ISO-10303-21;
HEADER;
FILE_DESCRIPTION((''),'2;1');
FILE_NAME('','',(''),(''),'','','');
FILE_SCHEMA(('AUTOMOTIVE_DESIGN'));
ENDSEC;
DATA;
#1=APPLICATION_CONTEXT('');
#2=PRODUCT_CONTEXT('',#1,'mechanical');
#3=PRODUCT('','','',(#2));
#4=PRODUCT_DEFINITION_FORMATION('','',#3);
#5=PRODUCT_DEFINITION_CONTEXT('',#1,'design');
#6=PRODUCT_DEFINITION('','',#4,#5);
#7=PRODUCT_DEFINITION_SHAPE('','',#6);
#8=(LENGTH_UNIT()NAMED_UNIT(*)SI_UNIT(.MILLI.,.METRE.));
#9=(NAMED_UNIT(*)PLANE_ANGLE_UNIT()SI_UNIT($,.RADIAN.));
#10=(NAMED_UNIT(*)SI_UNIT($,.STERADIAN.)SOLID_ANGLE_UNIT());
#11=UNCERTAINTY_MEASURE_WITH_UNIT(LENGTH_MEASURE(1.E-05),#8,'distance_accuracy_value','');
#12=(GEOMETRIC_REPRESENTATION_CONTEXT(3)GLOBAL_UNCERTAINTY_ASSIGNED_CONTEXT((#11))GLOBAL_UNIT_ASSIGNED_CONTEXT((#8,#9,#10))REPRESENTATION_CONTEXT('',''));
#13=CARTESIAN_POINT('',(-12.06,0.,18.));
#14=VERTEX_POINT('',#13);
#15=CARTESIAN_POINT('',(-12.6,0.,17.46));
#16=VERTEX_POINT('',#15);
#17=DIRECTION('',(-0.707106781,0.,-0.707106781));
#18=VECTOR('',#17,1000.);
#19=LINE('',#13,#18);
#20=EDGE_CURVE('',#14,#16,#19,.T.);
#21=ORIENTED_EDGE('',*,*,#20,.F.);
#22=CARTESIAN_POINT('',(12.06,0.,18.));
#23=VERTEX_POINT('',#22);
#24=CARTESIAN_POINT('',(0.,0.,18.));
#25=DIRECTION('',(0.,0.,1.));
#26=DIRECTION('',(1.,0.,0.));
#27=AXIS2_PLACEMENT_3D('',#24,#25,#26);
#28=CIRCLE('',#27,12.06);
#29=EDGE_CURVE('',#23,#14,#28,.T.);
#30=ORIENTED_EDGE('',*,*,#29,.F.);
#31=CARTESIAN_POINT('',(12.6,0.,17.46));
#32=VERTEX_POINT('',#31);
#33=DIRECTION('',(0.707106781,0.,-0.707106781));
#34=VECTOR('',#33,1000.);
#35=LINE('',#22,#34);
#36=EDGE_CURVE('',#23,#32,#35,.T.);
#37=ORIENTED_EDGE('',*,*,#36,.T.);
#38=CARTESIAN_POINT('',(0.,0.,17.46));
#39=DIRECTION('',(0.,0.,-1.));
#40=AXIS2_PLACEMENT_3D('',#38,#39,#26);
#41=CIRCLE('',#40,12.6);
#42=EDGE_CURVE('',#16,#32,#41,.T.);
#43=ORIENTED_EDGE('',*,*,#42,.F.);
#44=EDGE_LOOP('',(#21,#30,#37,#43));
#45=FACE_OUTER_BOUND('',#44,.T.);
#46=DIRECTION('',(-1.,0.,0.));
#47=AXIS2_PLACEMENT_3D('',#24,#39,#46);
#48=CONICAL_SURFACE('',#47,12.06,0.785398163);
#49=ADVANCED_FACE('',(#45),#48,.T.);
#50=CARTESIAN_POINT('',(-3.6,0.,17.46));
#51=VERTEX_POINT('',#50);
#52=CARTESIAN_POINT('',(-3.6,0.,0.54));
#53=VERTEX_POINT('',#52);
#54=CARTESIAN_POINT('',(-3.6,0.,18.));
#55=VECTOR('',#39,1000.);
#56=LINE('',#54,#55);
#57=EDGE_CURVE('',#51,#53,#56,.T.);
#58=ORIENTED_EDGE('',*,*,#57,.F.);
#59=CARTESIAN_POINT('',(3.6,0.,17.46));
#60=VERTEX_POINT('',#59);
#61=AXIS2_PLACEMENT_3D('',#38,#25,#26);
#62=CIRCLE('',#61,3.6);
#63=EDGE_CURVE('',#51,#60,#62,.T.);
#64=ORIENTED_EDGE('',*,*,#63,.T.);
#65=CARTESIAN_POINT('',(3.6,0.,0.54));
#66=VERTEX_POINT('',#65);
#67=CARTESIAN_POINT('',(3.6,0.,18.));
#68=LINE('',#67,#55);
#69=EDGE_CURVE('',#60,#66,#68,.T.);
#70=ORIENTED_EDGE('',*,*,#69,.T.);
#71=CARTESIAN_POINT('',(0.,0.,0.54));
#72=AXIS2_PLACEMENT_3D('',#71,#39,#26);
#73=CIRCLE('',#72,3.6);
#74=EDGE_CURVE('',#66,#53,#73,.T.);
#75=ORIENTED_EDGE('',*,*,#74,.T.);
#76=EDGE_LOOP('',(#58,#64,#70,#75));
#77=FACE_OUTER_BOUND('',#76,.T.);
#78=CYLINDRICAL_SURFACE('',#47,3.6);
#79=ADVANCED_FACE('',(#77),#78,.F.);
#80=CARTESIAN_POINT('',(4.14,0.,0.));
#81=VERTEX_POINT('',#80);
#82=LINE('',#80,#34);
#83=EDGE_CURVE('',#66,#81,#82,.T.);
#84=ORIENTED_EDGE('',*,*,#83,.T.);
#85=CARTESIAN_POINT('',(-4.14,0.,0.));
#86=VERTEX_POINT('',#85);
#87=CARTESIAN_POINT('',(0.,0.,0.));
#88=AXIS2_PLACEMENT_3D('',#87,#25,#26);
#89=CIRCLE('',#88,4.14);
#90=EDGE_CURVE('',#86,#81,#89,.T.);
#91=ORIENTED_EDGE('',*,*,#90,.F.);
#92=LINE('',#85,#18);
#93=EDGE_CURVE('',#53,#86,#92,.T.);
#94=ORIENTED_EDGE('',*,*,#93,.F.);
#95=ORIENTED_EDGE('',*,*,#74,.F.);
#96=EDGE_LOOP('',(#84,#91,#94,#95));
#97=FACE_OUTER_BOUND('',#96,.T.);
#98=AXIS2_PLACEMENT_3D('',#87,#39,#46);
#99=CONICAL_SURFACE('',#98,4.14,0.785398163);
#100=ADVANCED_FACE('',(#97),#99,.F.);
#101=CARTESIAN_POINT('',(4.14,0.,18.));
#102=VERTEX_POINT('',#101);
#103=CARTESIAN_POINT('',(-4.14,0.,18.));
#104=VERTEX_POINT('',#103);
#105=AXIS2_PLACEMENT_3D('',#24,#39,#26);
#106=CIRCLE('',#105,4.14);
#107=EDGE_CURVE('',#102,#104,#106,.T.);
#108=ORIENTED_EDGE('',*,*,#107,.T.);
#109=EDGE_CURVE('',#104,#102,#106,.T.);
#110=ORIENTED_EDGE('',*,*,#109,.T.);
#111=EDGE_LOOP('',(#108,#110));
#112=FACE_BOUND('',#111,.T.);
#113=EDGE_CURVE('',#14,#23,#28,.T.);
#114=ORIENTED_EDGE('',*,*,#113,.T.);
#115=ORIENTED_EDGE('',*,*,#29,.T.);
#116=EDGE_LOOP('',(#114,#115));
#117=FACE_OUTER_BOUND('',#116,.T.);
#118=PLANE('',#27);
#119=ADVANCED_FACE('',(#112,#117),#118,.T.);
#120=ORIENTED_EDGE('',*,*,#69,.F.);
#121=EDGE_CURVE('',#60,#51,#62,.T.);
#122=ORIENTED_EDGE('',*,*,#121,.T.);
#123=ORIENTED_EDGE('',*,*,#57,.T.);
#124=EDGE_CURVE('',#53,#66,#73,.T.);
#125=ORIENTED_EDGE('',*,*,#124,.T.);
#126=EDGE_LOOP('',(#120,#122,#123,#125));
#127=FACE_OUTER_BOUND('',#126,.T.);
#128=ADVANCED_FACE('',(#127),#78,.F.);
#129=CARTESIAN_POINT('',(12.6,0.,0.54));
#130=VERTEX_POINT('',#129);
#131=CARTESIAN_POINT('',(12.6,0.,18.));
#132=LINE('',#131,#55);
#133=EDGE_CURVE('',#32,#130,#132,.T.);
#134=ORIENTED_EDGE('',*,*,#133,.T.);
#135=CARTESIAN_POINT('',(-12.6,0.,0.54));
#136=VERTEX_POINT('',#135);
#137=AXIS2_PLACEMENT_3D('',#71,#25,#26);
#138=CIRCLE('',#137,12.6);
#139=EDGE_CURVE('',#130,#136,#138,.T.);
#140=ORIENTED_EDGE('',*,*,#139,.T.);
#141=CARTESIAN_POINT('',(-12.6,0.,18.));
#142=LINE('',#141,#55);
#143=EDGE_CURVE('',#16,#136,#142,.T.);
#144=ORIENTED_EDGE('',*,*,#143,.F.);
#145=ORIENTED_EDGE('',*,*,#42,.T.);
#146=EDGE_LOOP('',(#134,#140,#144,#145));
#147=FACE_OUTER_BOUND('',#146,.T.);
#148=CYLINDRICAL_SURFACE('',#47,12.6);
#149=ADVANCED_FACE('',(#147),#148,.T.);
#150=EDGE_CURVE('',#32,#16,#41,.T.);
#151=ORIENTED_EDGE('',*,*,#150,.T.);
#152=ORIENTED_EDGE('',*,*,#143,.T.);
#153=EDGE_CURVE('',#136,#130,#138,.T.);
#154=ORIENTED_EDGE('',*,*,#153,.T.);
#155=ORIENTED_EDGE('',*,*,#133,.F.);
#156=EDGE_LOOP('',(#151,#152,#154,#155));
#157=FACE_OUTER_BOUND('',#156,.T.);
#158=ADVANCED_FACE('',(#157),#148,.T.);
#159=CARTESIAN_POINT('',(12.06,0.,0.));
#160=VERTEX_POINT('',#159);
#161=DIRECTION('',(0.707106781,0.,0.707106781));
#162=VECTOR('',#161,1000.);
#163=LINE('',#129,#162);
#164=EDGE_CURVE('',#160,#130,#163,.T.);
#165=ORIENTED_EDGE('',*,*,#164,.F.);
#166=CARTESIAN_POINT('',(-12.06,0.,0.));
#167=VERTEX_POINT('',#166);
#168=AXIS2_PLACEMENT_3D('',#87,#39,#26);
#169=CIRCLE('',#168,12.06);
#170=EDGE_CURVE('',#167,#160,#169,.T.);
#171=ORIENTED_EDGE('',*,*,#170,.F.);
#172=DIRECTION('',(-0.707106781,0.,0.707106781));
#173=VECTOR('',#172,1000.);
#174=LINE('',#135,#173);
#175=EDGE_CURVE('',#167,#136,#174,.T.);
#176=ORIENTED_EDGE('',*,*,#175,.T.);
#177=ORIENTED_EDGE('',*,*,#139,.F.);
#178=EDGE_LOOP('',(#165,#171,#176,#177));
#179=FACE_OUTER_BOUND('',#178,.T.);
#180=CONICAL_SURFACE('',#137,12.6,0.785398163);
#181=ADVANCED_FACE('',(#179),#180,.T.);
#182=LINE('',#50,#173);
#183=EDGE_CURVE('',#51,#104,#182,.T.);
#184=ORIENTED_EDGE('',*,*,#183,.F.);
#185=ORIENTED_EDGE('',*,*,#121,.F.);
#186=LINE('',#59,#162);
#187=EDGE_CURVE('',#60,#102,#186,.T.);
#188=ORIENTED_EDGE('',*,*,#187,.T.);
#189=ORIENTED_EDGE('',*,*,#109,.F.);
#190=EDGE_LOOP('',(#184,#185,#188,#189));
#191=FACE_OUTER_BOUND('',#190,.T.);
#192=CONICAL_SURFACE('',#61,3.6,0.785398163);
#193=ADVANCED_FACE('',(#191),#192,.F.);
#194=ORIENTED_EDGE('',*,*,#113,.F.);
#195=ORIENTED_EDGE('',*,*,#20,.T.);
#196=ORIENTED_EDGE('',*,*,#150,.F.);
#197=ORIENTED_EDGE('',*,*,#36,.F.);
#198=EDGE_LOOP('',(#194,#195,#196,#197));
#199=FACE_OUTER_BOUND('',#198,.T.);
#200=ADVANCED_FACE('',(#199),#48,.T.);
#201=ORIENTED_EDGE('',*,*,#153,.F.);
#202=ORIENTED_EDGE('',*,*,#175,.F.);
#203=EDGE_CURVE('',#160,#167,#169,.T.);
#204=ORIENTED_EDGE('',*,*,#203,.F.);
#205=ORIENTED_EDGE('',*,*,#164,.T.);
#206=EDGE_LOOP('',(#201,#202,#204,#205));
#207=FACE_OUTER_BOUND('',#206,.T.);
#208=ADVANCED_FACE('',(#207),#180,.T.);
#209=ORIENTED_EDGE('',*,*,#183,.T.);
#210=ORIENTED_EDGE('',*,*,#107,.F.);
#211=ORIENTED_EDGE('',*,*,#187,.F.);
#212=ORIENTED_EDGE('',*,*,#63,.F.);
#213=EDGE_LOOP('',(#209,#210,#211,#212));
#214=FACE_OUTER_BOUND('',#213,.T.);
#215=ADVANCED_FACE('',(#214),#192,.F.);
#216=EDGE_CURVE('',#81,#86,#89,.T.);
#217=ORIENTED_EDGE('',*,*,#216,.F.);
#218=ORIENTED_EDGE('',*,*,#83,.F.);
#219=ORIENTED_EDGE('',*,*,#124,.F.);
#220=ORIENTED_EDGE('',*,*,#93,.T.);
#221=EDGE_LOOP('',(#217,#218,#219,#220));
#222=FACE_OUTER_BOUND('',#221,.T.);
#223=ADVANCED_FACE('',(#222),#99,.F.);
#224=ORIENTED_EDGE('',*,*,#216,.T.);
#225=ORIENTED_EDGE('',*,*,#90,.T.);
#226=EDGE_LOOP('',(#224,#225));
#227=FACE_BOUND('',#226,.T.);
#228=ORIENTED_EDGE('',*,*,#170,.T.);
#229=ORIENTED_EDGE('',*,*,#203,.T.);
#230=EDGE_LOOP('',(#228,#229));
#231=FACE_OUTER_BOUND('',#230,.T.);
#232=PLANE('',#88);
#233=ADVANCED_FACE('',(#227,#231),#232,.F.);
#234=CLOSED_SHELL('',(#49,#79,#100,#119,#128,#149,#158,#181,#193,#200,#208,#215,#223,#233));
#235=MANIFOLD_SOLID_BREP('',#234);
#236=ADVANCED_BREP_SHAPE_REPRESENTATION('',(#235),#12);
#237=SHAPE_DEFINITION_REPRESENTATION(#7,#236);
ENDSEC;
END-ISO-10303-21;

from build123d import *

# Parameters (mm, degrees)
SKETCH1_R           = 12.6
SKETCH1_R_2         = 3.6
BOSS_EXTRUDE1_DEPTH = 18
CHAMFER1_SIZE       = 0.54


with BuildPart() as part:
    # Sketch1 → Boss-Extrude1 (new body)
    with BuildSketch(Plane.XY):
        Circle(SKETCH1_R)
        Circle(SKETCH1_R_2, mode=Mode.SUBTRACT)
    extrude(amount=BOSS_EXTRUDE1_DEPTH)

    # Chamfer1
    chamfer1_edges = [part.edges().sort_by_distance(p)[0] for p in [
        (-12.6, 0, 0),
        (-12.6, 0, 18),
        (-3.6, 0, 0),
        (-3.6, 0, 18),
    ]]
    chamfer(chamfer1_edges, length=CHAMFER1_SIZE)


solid = part.part
